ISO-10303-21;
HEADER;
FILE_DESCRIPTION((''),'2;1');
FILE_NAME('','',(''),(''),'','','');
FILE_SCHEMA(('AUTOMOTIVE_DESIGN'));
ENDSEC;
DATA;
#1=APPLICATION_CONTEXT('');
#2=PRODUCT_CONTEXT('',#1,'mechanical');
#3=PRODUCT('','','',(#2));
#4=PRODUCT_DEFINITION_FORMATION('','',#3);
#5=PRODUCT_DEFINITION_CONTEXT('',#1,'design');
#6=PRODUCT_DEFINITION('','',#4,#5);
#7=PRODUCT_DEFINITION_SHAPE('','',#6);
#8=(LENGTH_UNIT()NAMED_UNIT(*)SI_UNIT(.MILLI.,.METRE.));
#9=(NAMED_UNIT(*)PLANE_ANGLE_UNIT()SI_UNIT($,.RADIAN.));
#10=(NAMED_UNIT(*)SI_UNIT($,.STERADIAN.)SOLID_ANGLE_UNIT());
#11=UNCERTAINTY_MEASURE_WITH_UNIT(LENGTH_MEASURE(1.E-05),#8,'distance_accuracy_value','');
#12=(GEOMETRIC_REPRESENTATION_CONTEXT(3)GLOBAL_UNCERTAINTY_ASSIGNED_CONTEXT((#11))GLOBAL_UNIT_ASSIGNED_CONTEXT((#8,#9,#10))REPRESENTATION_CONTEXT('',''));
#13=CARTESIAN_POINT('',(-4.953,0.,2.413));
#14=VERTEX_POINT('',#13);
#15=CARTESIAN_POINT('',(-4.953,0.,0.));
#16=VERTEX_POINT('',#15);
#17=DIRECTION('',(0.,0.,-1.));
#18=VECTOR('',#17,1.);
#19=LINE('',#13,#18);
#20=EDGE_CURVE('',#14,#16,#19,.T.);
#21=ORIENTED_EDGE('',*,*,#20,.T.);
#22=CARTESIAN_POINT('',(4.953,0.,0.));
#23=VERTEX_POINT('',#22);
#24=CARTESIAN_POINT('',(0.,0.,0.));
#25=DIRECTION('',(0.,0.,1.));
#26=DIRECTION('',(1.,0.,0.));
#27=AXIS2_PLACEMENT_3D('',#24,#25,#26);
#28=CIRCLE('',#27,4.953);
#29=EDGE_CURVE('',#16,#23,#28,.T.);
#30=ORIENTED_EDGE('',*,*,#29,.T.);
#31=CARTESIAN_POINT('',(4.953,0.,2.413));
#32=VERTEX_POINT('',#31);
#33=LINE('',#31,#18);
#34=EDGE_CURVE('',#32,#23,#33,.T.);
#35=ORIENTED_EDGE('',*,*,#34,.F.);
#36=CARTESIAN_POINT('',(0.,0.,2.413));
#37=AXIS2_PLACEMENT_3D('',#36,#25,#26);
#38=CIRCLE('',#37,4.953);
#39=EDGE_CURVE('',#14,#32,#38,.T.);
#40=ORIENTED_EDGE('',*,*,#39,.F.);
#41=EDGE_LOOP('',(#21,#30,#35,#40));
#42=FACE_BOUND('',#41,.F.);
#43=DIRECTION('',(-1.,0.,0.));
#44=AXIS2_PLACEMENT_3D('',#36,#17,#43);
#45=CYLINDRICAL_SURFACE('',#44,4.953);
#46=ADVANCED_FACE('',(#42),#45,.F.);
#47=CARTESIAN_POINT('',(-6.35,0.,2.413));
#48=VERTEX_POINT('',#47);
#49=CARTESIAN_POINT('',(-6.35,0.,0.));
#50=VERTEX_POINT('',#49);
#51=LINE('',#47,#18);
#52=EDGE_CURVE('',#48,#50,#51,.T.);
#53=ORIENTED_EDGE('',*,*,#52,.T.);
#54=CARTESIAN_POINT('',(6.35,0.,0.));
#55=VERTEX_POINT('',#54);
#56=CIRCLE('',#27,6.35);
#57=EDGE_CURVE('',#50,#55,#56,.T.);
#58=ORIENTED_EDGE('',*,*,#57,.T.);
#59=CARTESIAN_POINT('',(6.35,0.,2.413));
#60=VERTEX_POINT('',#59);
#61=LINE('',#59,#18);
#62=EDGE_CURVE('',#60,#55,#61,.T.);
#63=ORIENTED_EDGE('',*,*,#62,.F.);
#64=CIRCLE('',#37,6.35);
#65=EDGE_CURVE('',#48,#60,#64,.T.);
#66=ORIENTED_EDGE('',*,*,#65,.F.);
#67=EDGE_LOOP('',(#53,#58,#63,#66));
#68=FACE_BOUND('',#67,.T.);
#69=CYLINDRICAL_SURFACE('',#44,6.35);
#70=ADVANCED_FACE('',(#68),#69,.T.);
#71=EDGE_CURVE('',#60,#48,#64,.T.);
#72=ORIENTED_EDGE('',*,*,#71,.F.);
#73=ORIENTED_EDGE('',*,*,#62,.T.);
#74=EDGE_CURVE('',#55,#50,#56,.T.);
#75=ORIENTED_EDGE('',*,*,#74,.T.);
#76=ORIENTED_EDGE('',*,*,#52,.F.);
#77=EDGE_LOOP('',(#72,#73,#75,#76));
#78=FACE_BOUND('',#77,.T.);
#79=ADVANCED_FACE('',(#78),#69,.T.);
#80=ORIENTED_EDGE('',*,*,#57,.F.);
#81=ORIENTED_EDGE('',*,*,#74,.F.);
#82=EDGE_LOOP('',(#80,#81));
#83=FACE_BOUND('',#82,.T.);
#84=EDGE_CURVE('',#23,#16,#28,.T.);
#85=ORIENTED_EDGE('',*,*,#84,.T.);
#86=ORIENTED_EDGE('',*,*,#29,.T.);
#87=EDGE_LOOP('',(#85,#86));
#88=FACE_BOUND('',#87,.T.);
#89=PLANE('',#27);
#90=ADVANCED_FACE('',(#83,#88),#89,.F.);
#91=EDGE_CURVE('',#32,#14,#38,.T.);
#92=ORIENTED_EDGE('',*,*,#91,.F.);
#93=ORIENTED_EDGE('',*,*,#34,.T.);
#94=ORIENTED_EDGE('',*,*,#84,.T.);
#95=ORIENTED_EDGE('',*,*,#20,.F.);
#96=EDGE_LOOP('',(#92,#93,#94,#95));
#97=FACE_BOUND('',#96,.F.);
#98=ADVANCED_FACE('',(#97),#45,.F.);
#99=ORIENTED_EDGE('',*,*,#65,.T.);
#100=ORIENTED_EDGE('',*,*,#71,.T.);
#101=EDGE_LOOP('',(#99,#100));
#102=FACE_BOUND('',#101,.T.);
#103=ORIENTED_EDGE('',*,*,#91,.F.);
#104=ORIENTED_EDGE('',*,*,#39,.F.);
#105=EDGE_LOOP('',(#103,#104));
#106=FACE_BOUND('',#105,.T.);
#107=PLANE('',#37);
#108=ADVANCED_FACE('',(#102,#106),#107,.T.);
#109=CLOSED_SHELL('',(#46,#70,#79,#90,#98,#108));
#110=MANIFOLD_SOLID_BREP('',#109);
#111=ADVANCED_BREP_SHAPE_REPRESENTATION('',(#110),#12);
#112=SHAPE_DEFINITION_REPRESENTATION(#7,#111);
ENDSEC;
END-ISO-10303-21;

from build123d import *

# Parameters (mm, degrees)
BUSH_RING_PROFILE_0_500_X_0_390_R   = 6.35
BUSH_RING_PROFILE_0_500_X_0_390_R_2 = 4.953
BUSH_RING_0_095_THICK_DEPTH         = 2.413


with BuildPart() as part:
    # Bush Ring Profile Ø0.500 x Ø0.390 → Bush Ring 0.095 Thick (new body)
    with BuildSketch(Plane.XY):
        Circle(BUSH_RING_PROFILE_0_500_X_0_390_R)
        Circle(BUSH_RING_PROFILE_0_500_X_0_390_R_2, mode=Mode.SUBTRACT)
    extrude(amount=BUSH_RING_0_095_THICK_DEPTH)


solid = part.part
